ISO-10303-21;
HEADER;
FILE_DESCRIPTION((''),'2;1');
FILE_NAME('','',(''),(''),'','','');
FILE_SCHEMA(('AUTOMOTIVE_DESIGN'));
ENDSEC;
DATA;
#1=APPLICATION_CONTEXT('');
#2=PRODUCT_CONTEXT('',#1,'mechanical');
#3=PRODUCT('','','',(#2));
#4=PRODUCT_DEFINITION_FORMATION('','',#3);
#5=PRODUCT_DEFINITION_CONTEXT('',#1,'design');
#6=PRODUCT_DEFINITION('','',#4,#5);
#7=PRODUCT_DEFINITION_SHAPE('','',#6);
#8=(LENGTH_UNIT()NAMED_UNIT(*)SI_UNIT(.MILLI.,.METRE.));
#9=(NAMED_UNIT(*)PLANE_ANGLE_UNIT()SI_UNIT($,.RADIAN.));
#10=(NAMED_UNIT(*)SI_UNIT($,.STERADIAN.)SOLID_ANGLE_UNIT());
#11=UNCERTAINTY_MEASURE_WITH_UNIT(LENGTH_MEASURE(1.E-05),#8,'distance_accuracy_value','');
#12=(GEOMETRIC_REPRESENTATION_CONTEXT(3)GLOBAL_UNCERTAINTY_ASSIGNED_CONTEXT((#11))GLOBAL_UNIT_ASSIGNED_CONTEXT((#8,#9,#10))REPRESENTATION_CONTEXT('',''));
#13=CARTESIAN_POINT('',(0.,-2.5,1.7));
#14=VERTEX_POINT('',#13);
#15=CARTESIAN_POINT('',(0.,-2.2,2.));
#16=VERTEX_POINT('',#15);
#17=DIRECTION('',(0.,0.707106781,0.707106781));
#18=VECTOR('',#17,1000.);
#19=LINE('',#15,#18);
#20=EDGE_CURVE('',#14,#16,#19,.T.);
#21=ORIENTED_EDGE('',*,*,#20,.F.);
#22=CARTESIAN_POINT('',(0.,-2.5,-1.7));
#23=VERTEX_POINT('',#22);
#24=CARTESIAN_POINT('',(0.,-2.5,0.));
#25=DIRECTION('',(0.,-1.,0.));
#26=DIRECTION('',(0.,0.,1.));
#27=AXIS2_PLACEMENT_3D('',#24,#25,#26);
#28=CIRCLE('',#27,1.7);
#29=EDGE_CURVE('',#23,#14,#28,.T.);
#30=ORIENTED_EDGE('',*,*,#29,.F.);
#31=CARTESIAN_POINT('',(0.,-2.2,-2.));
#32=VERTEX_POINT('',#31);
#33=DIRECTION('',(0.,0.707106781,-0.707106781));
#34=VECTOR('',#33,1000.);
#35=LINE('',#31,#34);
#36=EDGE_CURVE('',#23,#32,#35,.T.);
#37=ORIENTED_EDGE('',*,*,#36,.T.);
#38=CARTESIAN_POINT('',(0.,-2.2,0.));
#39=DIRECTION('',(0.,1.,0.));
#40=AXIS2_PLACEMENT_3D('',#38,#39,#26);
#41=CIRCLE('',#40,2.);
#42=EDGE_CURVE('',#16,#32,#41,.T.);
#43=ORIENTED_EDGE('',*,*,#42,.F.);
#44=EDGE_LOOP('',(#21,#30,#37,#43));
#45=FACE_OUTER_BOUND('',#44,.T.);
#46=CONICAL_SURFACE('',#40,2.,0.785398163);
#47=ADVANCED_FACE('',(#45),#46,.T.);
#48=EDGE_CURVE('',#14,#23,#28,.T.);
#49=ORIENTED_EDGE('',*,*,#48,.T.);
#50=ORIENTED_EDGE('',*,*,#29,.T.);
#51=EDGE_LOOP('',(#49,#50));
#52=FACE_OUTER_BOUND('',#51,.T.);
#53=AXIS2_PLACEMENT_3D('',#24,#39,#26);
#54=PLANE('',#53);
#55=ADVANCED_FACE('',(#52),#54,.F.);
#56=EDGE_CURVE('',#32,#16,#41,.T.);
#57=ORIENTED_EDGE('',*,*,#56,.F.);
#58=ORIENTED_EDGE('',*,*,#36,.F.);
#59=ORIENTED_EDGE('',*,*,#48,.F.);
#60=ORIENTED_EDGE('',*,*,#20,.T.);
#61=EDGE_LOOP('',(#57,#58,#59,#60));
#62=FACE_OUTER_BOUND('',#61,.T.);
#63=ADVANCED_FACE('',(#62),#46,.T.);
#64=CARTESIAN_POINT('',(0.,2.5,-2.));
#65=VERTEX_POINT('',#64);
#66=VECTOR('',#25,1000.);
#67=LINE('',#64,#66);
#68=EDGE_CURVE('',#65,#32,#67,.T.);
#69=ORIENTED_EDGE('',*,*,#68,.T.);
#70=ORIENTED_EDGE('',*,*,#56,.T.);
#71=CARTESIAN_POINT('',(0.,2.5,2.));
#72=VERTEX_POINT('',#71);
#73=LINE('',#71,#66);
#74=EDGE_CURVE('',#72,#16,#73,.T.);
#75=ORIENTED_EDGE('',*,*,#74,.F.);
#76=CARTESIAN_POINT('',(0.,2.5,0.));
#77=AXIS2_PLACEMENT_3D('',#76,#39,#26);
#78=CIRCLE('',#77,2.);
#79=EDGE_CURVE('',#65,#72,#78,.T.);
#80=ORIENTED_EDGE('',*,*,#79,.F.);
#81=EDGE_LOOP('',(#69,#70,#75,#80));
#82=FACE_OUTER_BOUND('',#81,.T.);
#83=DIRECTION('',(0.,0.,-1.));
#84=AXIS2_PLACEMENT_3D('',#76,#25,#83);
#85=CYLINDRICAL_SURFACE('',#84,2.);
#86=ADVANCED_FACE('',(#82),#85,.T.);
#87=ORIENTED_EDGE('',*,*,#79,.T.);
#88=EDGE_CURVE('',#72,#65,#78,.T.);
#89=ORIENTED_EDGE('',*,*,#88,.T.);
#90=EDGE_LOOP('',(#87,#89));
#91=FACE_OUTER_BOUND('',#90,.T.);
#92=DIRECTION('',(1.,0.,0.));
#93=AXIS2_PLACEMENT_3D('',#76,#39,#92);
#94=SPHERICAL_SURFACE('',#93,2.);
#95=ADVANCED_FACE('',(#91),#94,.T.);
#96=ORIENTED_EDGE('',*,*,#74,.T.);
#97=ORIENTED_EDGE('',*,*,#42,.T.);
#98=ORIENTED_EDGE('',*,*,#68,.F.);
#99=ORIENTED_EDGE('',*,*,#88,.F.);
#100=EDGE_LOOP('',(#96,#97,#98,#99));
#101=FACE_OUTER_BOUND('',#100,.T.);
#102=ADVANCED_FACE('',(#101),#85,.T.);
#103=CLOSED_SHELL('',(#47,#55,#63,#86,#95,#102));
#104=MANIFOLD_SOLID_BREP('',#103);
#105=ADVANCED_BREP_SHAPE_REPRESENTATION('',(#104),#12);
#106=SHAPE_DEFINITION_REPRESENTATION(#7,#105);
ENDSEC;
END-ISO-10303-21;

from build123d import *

# Parameters (mm, degrees)
SKETCH1_R           = 2
BOSS_EXTRUDE1_DEPTH = 2.5
DOME1_FACE_RADIUS   = 2
DOME1_HEIGHT        = 2
CHAMFER1_SIZE       = 0.3


with BuildPart() as part:
    # Sketch1 → Boss-Extrude1 (new, symmetric)
    with BuildSketch(Plane(origin=(0, 0, 0), x_dir=(1, 0, 0), z_dir=(0, 1, 0))):
        with Locations(Location((0, 0, 0), (0, 0, 270))):
            Circle(SKETCH1_R)
    extrude(amount=BOSS_EXTRUDE1_DEPTH, both=True)

    # Dome1: a dome of height H over a round flat face of radius A is a cap of a sphere of radius (A * A + H * H) / (2 * H)
    dome1_r = (DOME1_FACE_RADIUS * DOME1_FACE_RADIUS + DOME1_HEIGHT * DOME1_HEIGHT) / (2 * DOME1_HEIGHT)
    dome1_base = Plane((0, 2.5, 0), z_dir=(0, 1, 0))
    with Locations(dome1_base.offset(DOME1_HEIGHT - dome1_r)):
        dome1_ball = Sphere(dome1_r, mode=Mode.PRIVATE)
    add(split(dome1_ball, bisect_by=dome1_base, keep=Keep.TOP, mode=Mode.PRIVATE))

    # Chamfer1
    chamfer1_edges = [part.edges().sort_by_distance(p)[0] for p in [
        (0, -2.5, -2),
    ]]
    chamfer(chamfer1_edges, length=CHAMFER1_SIZE)


solid = part.part
